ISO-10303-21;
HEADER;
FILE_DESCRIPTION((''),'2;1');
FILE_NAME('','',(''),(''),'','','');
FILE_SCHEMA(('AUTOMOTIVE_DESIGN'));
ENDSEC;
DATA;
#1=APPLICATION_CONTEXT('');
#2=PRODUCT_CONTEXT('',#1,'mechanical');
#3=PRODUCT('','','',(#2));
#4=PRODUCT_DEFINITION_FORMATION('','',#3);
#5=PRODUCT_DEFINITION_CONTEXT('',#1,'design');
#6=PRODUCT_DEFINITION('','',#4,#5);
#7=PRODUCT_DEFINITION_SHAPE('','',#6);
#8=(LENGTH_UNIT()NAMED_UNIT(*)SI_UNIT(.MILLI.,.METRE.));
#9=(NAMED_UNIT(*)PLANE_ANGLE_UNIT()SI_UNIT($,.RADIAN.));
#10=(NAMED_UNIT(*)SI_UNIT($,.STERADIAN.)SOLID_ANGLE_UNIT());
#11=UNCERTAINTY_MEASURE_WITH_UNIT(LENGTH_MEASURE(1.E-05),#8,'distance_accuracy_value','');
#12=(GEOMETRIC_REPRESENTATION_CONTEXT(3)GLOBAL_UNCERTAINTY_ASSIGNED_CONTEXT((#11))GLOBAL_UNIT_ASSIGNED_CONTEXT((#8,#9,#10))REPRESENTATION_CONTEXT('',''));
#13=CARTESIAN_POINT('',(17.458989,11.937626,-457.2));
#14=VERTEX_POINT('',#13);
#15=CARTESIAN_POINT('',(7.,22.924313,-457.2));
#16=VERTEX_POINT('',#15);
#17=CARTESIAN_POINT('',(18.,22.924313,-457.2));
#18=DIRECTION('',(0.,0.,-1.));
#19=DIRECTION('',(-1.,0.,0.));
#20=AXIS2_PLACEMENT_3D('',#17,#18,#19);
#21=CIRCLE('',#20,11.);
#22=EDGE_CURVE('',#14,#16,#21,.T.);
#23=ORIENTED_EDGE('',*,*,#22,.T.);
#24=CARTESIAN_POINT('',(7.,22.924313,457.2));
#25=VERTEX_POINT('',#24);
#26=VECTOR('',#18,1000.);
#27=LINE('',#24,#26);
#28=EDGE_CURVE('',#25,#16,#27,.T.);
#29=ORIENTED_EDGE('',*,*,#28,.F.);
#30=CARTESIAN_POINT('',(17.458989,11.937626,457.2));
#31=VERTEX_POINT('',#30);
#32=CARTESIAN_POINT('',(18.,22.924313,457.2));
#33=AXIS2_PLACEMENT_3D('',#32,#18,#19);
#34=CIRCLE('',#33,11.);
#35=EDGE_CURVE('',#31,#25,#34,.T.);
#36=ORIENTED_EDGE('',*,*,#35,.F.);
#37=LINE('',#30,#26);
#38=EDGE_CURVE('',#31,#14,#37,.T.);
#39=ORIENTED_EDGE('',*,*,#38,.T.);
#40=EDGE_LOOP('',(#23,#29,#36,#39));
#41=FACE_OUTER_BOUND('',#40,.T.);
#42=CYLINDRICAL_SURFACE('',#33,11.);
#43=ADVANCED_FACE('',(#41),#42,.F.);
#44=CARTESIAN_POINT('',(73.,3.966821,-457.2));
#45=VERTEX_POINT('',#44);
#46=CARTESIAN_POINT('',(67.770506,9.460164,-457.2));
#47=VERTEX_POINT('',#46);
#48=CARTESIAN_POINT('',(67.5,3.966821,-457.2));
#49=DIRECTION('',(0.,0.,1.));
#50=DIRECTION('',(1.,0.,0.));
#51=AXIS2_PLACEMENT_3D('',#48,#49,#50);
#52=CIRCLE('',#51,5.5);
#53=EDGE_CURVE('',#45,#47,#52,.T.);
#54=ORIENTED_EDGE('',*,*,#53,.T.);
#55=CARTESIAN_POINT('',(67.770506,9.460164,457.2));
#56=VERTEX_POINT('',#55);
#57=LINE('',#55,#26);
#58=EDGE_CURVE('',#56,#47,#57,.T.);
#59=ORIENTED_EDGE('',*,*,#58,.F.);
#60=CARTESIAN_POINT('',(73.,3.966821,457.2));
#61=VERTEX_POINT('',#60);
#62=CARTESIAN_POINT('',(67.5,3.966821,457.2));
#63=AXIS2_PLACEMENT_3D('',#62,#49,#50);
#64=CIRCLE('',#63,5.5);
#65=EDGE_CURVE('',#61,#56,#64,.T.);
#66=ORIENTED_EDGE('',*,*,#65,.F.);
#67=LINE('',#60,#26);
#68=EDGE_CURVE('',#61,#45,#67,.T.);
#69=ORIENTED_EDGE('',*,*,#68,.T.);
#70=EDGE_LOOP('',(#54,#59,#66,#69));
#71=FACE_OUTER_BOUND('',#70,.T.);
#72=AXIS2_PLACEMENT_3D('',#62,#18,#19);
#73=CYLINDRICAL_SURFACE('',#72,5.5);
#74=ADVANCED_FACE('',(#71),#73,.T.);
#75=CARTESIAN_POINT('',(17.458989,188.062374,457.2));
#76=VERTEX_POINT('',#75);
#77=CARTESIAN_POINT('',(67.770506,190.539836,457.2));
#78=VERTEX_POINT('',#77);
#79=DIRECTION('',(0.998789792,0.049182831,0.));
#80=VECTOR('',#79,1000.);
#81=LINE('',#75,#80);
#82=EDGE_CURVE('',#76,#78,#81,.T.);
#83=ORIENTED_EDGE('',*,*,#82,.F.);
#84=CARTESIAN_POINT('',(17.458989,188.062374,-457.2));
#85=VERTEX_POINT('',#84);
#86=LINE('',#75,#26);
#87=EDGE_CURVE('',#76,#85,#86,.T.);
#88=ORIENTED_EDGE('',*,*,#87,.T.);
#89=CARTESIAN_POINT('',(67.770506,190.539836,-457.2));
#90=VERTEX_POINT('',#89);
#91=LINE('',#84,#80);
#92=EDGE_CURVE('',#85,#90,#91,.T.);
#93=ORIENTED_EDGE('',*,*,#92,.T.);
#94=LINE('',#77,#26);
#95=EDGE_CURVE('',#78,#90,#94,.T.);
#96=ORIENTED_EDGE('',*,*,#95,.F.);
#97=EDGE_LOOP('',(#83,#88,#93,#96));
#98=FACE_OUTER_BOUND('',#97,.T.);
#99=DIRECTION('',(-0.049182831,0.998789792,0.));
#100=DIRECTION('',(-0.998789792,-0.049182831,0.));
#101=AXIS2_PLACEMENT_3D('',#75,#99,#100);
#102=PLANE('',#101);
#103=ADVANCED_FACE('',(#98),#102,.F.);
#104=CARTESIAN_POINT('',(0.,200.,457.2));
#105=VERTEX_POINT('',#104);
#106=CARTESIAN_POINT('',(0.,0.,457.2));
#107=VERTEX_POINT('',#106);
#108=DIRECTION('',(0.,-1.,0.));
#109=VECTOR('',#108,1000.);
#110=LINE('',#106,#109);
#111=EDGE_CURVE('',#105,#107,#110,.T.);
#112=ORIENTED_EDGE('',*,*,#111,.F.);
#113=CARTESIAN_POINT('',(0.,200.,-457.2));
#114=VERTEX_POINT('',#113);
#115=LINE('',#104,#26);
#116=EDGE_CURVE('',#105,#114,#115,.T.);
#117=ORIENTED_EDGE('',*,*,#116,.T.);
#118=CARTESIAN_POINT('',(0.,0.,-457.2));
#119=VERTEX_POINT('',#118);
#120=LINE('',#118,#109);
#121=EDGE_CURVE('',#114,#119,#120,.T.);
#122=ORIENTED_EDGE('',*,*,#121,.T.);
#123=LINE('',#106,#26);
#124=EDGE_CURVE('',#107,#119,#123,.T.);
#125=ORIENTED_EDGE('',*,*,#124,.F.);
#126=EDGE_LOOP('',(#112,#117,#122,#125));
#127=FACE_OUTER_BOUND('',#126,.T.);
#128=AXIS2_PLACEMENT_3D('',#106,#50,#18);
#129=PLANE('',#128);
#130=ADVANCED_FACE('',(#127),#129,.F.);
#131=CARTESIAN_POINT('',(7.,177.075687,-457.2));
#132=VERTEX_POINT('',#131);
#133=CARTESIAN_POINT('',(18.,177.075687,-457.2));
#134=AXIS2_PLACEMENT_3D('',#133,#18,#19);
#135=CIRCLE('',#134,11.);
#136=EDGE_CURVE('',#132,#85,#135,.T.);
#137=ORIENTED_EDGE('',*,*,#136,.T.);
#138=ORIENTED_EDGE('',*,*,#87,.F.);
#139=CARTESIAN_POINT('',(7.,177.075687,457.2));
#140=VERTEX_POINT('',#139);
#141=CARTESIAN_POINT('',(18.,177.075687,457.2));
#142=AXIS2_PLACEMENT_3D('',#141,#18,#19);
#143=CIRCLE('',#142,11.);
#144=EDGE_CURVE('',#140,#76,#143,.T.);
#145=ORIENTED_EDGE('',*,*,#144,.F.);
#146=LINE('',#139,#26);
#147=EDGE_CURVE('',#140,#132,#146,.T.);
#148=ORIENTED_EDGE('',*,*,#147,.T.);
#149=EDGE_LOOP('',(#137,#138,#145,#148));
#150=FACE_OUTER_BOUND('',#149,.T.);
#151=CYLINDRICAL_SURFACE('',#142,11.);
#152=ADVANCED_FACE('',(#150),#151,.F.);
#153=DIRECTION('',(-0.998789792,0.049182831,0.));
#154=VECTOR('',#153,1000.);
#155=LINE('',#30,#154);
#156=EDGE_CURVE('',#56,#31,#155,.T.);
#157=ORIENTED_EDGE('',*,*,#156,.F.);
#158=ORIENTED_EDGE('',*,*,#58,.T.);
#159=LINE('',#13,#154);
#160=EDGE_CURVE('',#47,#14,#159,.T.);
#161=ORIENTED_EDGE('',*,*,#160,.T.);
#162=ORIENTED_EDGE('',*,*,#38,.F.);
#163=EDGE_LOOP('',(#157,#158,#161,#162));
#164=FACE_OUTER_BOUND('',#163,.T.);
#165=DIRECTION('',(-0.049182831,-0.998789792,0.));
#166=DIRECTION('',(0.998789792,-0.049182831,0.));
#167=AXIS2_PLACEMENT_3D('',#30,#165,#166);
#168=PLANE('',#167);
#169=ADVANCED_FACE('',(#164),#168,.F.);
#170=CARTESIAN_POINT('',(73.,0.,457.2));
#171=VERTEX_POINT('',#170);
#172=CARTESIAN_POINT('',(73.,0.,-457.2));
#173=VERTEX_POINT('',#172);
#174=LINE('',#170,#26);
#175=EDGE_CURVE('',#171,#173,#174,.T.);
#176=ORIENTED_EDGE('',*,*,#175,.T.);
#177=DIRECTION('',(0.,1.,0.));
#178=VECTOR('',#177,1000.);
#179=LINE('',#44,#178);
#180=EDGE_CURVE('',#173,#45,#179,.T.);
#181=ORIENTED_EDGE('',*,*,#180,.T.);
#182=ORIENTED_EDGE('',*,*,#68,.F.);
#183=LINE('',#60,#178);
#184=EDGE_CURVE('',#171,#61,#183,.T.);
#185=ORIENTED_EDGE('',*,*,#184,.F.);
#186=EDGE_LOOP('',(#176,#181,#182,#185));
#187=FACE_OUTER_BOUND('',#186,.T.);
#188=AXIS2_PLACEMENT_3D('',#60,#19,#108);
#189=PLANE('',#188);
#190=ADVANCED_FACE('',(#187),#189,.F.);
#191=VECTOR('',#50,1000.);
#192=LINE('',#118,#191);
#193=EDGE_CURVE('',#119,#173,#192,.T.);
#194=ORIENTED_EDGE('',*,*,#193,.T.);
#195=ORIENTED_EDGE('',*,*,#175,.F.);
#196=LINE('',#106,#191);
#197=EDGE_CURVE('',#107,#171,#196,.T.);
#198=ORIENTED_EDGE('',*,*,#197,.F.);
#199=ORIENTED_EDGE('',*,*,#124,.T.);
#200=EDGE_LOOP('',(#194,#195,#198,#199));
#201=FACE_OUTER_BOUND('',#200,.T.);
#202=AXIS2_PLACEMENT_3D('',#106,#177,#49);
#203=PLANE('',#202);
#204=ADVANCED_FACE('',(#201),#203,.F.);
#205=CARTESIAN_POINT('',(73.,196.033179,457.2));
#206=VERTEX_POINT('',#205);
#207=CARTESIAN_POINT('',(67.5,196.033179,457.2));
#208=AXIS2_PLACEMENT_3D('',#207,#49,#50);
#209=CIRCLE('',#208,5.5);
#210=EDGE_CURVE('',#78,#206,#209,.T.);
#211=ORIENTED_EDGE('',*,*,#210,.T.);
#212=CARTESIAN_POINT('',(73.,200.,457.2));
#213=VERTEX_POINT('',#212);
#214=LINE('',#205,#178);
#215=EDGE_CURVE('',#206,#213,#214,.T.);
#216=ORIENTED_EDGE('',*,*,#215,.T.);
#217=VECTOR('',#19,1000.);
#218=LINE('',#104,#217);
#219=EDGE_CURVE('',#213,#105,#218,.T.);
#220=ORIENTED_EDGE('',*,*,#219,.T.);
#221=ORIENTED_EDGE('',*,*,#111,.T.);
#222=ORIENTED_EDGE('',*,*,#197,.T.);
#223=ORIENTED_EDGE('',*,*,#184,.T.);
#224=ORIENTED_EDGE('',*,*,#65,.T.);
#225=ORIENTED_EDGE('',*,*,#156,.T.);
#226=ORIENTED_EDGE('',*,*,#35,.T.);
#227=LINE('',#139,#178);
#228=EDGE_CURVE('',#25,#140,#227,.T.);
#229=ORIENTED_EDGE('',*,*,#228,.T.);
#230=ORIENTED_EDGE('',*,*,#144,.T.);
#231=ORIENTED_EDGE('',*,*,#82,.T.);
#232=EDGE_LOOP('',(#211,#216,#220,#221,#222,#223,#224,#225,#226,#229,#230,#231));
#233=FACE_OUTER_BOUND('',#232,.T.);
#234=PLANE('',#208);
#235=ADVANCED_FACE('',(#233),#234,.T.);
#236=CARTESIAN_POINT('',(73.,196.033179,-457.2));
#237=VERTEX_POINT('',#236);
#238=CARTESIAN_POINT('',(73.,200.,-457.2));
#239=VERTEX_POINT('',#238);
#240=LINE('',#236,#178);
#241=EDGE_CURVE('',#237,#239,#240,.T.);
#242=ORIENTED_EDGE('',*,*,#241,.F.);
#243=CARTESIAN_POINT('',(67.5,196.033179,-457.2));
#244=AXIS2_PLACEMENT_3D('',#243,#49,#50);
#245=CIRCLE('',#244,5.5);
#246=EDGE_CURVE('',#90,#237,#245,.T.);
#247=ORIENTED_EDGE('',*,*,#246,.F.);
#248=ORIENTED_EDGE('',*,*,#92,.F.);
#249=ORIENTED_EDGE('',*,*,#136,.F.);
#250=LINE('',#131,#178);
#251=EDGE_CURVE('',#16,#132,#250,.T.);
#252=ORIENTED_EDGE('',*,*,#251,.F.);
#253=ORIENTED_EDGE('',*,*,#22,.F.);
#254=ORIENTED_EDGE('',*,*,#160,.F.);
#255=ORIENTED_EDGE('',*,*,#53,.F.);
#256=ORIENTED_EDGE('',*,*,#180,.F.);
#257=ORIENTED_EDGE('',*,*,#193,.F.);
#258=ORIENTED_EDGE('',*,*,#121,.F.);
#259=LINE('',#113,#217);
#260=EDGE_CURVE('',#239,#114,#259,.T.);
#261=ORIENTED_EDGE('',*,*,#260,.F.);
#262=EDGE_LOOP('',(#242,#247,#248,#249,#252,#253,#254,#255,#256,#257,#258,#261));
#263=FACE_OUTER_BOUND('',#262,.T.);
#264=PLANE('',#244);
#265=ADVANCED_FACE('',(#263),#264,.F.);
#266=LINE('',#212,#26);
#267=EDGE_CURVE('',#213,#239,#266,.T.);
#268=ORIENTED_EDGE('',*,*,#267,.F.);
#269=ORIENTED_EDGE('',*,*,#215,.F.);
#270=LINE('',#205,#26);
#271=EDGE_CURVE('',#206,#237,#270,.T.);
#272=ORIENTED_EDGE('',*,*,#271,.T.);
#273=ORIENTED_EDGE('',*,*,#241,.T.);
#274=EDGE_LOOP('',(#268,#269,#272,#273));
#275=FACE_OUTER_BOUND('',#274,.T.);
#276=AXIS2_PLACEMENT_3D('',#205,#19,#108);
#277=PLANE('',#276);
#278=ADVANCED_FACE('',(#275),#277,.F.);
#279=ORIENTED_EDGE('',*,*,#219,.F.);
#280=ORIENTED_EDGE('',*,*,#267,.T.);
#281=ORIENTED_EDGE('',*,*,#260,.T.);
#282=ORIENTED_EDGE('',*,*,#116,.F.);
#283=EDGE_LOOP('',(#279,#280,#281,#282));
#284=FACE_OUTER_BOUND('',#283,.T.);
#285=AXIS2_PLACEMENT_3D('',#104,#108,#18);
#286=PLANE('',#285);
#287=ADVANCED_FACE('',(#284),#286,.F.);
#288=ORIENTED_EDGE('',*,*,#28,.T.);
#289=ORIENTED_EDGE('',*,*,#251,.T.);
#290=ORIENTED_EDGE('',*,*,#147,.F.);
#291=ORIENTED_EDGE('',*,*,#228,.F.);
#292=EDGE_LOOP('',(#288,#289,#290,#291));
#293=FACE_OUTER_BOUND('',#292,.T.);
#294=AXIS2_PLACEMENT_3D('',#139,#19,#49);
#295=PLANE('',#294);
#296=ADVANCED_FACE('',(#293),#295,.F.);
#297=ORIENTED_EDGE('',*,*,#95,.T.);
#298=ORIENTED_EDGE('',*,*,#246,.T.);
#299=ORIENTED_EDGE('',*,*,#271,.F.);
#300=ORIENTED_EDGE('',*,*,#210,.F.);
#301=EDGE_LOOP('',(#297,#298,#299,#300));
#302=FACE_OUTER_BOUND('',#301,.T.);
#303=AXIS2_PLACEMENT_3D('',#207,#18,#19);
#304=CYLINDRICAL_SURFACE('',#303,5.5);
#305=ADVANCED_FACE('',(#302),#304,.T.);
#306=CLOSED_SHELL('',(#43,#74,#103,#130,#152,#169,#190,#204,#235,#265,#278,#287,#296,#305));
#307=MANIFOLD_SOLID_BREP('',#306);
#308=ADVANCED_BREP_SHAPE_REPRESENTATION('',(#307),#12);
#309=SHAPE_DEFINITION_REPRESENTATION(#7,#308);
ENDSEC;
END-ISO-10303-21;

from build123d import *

# Parameters (mm, degrees)
BOSS_EXTRUDE1_DEPTH = 457.2


with BuildPart() as part:
    # Sketch1 → Boss-Extrude1 (new, symmetric)
    with BuildSketch(Plane(origin=(28.211262136, 0, 0), x_dir=(-1, 0, 0), z_dir=(0, 0, 1))):
        with BuildLine():
            Line((28.211262136, 0), (28.211262136, -200))
            Line((28.211262136, -200), (-44.788737864, -200))
            Line((-44.788737864, -200), (-44.788737864, -196.033179359))
            ThreePointArc((-44.788737864, -196.033179359), (-43.272315441, -192.240936001), (-39.559243433, -190.539835501))
            Line((-39.559243433, -190.539835501), (10.752273273, -188.062374452))
            ThreePointArc((10.752273273, -188.062374452), (18.17841729, -184.660173452), (21.211262136, -177.075686736))
            Line((21.211262136, -177.075686736), (21.211262136, -22.924313264))
            ThreePointArc((21.211262136, -22.924313264), (18.17841729, -15.339826548), (10.752273273, -11.937625548))
            Line((10.752273273, -11.937625548), (-39.559243433, -9.460164499))
            ThreePointArc((-39.559243433, -9.460164499), (-43.272315441, -7.759063999), (-44.788737864, -3.966820641))
            Line((-44.788737864, -3.966820641), (-44.788737864, 0))
            Line((-44.788737864, 0), (28.211262136, 0))
        make_face()
    extrude(amount=BOSS_EXTRUDE1_DEPTH, both=True)


solid = part.part
